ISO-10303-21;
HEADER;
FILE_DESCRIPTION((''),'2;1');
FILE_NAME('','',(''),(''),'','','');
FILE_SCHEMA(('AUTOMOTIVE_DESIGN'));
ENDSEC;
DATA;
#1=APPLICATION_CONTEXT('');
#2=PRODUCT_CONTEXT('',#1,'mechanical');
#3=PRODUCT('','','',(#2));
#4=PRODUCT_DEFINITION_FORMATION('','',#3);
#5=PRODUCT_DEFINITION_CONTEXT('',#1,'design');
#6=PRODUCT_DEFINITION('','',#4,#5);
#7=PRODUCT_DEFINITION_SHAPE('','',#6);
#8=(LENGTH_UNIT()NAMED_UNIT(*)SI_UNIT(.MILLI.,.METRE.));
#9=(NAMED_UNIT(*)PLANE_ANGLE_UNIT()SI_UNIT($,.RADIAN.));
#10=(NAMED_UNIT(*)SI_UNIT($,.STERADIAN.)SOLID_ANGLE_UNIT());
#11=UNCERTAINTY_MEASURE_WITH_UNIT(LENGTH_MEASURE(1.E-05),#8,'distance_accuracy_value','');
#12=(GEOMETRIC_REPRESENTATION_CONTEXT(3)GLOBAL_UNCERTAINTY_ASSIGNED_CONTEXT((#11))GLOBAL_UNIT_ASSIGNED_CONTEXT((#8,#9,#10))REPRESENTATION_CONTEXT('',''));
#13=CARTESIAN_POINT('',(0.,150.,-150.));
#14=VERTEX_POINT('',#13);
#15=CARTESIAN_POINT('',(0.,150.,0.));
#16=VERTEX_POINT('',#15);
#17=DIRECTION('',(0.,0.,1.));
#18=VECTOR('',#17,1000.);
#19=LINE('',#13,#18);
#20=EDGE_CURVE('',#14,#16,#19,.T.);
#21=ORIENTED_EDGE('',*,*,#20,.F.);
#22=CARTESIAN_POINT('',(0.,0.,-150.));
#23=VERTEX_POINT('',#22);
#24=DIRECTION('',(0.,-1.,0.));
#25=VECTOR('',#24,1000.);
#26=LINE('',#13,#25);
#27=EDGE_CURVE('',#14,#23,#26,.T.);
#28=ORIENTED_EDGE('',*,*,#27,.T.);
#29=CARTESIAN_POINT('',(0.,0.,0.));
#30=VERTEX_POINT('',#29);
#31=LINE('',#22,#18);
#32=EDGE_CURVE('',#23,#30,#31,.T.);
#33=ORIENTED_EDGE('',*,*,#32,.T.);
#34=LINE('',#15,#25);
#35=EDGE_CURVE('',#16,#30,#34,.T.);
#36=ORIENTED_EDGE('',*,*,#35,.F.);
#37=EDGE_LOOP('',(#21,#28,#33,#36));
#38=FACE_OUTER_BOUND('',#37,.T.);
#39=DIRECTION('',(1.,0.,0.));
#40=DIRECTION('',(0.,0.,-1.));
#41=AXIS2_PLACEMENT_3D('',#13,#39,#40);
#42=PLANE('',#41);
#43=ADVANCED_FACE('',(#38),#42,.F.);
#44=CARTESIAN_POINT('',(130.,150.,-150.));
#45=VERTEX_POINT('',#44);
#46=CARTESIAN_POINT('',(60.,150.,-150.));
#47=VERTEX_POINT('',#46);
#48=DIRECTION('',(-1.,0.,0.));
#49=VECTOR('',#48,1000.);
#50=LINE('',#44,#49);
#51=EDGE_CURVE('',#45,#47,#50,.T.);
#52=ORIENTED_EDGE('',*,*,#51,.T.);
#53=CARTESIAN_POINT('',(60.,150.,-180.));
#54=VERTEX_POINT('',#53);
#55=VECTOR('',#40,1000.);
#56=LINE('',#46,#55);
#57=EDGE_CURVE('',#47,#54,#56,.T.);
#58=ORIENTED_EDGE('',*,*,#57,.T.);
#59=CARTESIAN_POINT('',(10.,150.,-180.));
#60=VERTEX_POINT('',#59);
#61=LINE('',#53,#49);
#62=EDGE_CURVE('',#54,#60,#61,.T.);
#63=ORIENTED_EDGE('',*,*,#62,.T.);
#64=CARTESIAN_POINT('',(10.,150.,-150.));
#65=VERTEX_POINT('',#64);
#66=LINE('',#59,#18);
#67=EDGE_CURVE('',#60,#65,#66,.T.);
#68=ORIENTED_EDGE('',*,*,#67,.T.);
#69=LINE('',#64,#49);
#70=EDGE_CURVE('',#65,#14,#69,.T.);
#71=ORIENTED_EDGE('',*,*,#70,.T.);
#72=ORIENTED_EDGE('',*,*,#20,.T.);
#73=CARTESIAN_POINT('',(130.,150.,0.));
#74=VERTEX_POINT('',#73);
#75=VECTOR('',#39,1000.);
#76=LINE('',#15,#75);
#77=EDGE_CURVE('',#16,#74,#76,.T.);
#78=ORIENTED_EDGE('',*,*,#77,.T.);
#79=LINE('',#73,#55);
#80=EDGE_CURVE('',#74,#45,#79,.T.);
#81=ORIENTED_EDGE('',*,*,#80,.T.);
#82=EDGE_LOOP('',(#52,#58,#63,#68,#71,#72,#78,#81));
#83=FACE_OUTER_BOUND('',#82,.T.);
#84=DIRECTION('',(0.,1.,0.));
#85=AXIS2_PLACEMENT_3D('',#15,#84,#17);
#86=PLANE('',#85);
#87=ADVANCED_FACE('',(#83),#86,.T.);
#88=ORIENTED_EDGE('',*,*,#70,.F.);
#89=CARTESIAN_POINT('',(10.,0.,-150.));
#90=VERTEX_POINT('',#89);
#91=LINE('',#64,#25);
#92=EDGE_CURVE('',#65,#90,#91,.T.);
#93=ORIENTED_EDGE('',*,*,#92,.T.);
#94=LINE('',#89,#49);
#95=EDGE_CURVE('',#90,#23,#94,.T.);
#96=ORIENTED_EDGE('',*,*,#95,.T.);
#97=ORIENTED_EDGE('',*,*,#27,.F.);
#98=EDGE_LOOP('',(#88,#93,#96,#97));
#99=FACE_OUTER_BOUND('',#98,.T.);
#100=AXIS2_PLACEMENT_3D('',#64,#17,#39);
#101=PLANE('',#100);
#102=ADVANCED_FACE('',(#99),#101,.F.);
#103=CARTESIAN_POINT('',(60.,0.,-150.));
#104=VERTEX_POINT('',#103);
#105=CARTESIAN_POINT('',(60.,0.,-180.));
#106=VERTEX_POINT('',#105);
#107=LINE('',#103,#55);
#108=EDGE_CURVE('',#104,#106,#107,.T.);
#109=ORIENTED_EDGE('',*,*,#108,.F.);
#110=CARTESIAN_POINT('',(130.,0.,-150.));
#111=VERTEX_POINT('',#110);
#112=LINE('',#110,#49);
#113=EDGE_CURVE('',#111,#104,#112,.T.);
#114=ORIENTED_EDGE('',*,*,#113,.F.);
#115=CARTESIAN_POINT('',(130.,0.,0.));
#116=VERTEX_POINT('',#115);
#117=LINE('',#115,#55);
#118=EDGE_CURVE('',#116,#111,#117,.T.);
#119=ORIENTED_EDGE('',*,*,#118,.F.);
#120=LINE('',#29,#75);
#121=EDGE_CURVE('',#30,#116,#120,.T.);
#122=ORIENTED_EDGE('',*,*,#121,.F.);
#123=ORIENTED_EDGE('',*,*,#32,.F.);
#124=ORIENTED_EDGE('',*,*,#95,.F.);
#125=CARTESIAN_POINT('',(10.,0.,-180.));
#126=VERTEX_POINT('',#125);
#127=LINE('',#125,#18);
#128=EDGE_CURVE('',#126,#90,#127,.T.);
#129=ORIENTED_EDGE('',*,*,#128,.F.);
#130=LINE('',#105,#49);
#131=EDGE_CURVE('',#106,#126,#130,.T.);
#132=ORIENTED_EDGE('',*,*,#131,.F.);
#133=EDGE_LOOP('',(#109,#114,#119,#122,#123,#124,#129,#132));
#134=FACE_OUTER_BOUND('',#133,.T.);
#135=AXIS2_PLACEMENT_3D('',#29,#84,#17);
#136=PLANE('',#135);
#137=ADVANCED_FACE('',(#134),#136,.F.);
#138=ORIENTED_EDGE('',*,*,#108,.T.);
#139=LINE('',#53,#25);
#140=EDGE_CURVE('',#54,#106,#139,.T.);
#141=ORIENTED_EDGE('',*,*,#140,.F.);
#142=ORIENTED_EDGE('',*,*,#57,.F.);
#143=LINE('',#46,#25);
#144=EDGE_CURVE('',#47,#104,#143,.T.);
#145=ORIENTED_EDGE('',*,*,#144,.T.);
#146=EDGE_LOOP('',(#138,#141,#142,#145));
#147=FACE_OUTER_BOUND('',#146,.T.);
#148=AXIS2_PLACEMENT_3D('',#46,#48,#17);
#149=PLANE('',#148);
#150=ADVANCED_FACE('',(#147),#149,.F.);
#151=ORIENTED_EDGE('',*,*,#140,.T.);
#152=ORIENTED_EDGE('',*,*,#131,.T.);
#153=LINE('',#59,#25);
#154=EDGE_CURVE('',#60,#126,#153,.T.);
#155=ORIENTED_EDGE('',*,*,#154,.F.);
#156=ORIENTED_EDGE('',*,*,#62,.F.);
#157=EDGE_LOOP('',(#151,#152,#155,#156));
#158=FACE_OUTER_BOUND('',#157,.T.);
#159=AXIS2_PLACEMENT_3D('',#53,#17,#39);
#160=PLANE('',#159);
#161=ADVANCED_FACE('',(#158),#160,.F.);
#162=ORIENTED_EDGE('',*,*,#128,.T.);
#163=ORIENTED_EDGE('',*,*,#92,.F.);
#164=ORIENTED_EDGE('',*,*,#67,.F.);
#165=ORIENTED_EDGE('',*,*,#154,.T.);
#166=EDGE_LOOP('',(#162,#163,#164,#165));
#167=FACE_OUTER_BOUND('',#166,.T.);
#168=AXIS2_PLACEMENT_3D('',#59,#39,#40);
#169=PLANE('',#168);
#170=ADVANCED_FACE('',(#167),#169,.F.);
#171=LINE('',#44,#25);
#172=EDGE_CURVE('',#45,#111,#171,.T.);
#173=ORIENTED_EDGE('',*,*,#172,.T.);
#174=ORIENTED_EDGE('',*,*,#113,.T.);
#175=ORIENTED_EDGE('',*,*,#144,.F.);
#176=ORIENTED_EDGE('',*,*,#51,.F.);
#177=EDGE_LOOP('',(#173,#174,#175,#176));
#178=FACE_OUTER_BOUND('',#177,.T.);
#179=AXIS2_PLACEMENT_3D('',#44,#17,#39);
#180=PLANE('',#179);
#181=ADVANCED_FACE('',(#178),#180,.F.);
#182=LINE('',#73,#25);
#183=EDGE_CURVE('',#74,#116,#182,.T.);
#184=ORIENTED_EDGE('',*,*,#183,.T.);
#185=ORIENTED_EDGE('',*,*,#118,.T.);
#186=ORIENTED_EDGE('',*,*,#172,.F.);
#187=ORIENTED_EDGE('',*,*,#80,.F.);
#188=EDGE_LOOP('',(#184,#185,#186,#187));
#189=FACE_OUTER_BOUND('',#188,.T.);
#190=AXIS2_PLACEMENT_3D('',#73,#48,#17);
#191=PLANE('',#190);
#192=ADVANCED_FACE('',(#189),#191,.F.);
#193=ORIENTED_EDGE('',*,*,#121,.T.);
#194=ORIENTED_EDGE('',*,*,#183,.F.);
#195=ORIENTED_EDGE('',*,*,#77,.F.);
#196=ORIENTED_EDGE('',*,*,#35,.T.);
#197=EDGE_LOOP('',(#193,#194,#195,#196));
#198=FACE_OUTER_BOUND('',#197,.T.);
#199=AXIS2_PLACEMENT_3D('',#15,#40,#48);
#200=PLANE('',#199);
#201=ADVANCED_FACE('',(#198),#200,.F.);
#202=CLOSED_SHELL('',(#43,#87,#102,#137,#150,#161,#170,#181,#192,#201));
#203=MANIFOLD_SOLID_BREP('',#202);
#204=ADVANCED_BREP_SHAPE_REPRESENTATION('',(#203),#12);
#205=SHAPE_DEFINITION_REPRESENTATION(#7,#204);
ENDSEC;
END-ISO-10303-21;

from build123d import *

# Parameters (mm, degrees)
EXTRUDE_1_DEPTH = 150


with BuildPart() as part:
    # 草图1 → 凸台-拉伸1 (new body)
    with BuildSketch(Plane(origin=(0, 0, 0), x_dir=(1, 0, 0), z_dir=(0, 1, 0))):
        Polygon((0, 0), (130, 0), (130, 150), (60, 150), (60, 180), (10, 180), (10, 150), (0, 150), align=None)
    extrude(amount=EXTRUDE_1_DEPTH)


solid = part.part
